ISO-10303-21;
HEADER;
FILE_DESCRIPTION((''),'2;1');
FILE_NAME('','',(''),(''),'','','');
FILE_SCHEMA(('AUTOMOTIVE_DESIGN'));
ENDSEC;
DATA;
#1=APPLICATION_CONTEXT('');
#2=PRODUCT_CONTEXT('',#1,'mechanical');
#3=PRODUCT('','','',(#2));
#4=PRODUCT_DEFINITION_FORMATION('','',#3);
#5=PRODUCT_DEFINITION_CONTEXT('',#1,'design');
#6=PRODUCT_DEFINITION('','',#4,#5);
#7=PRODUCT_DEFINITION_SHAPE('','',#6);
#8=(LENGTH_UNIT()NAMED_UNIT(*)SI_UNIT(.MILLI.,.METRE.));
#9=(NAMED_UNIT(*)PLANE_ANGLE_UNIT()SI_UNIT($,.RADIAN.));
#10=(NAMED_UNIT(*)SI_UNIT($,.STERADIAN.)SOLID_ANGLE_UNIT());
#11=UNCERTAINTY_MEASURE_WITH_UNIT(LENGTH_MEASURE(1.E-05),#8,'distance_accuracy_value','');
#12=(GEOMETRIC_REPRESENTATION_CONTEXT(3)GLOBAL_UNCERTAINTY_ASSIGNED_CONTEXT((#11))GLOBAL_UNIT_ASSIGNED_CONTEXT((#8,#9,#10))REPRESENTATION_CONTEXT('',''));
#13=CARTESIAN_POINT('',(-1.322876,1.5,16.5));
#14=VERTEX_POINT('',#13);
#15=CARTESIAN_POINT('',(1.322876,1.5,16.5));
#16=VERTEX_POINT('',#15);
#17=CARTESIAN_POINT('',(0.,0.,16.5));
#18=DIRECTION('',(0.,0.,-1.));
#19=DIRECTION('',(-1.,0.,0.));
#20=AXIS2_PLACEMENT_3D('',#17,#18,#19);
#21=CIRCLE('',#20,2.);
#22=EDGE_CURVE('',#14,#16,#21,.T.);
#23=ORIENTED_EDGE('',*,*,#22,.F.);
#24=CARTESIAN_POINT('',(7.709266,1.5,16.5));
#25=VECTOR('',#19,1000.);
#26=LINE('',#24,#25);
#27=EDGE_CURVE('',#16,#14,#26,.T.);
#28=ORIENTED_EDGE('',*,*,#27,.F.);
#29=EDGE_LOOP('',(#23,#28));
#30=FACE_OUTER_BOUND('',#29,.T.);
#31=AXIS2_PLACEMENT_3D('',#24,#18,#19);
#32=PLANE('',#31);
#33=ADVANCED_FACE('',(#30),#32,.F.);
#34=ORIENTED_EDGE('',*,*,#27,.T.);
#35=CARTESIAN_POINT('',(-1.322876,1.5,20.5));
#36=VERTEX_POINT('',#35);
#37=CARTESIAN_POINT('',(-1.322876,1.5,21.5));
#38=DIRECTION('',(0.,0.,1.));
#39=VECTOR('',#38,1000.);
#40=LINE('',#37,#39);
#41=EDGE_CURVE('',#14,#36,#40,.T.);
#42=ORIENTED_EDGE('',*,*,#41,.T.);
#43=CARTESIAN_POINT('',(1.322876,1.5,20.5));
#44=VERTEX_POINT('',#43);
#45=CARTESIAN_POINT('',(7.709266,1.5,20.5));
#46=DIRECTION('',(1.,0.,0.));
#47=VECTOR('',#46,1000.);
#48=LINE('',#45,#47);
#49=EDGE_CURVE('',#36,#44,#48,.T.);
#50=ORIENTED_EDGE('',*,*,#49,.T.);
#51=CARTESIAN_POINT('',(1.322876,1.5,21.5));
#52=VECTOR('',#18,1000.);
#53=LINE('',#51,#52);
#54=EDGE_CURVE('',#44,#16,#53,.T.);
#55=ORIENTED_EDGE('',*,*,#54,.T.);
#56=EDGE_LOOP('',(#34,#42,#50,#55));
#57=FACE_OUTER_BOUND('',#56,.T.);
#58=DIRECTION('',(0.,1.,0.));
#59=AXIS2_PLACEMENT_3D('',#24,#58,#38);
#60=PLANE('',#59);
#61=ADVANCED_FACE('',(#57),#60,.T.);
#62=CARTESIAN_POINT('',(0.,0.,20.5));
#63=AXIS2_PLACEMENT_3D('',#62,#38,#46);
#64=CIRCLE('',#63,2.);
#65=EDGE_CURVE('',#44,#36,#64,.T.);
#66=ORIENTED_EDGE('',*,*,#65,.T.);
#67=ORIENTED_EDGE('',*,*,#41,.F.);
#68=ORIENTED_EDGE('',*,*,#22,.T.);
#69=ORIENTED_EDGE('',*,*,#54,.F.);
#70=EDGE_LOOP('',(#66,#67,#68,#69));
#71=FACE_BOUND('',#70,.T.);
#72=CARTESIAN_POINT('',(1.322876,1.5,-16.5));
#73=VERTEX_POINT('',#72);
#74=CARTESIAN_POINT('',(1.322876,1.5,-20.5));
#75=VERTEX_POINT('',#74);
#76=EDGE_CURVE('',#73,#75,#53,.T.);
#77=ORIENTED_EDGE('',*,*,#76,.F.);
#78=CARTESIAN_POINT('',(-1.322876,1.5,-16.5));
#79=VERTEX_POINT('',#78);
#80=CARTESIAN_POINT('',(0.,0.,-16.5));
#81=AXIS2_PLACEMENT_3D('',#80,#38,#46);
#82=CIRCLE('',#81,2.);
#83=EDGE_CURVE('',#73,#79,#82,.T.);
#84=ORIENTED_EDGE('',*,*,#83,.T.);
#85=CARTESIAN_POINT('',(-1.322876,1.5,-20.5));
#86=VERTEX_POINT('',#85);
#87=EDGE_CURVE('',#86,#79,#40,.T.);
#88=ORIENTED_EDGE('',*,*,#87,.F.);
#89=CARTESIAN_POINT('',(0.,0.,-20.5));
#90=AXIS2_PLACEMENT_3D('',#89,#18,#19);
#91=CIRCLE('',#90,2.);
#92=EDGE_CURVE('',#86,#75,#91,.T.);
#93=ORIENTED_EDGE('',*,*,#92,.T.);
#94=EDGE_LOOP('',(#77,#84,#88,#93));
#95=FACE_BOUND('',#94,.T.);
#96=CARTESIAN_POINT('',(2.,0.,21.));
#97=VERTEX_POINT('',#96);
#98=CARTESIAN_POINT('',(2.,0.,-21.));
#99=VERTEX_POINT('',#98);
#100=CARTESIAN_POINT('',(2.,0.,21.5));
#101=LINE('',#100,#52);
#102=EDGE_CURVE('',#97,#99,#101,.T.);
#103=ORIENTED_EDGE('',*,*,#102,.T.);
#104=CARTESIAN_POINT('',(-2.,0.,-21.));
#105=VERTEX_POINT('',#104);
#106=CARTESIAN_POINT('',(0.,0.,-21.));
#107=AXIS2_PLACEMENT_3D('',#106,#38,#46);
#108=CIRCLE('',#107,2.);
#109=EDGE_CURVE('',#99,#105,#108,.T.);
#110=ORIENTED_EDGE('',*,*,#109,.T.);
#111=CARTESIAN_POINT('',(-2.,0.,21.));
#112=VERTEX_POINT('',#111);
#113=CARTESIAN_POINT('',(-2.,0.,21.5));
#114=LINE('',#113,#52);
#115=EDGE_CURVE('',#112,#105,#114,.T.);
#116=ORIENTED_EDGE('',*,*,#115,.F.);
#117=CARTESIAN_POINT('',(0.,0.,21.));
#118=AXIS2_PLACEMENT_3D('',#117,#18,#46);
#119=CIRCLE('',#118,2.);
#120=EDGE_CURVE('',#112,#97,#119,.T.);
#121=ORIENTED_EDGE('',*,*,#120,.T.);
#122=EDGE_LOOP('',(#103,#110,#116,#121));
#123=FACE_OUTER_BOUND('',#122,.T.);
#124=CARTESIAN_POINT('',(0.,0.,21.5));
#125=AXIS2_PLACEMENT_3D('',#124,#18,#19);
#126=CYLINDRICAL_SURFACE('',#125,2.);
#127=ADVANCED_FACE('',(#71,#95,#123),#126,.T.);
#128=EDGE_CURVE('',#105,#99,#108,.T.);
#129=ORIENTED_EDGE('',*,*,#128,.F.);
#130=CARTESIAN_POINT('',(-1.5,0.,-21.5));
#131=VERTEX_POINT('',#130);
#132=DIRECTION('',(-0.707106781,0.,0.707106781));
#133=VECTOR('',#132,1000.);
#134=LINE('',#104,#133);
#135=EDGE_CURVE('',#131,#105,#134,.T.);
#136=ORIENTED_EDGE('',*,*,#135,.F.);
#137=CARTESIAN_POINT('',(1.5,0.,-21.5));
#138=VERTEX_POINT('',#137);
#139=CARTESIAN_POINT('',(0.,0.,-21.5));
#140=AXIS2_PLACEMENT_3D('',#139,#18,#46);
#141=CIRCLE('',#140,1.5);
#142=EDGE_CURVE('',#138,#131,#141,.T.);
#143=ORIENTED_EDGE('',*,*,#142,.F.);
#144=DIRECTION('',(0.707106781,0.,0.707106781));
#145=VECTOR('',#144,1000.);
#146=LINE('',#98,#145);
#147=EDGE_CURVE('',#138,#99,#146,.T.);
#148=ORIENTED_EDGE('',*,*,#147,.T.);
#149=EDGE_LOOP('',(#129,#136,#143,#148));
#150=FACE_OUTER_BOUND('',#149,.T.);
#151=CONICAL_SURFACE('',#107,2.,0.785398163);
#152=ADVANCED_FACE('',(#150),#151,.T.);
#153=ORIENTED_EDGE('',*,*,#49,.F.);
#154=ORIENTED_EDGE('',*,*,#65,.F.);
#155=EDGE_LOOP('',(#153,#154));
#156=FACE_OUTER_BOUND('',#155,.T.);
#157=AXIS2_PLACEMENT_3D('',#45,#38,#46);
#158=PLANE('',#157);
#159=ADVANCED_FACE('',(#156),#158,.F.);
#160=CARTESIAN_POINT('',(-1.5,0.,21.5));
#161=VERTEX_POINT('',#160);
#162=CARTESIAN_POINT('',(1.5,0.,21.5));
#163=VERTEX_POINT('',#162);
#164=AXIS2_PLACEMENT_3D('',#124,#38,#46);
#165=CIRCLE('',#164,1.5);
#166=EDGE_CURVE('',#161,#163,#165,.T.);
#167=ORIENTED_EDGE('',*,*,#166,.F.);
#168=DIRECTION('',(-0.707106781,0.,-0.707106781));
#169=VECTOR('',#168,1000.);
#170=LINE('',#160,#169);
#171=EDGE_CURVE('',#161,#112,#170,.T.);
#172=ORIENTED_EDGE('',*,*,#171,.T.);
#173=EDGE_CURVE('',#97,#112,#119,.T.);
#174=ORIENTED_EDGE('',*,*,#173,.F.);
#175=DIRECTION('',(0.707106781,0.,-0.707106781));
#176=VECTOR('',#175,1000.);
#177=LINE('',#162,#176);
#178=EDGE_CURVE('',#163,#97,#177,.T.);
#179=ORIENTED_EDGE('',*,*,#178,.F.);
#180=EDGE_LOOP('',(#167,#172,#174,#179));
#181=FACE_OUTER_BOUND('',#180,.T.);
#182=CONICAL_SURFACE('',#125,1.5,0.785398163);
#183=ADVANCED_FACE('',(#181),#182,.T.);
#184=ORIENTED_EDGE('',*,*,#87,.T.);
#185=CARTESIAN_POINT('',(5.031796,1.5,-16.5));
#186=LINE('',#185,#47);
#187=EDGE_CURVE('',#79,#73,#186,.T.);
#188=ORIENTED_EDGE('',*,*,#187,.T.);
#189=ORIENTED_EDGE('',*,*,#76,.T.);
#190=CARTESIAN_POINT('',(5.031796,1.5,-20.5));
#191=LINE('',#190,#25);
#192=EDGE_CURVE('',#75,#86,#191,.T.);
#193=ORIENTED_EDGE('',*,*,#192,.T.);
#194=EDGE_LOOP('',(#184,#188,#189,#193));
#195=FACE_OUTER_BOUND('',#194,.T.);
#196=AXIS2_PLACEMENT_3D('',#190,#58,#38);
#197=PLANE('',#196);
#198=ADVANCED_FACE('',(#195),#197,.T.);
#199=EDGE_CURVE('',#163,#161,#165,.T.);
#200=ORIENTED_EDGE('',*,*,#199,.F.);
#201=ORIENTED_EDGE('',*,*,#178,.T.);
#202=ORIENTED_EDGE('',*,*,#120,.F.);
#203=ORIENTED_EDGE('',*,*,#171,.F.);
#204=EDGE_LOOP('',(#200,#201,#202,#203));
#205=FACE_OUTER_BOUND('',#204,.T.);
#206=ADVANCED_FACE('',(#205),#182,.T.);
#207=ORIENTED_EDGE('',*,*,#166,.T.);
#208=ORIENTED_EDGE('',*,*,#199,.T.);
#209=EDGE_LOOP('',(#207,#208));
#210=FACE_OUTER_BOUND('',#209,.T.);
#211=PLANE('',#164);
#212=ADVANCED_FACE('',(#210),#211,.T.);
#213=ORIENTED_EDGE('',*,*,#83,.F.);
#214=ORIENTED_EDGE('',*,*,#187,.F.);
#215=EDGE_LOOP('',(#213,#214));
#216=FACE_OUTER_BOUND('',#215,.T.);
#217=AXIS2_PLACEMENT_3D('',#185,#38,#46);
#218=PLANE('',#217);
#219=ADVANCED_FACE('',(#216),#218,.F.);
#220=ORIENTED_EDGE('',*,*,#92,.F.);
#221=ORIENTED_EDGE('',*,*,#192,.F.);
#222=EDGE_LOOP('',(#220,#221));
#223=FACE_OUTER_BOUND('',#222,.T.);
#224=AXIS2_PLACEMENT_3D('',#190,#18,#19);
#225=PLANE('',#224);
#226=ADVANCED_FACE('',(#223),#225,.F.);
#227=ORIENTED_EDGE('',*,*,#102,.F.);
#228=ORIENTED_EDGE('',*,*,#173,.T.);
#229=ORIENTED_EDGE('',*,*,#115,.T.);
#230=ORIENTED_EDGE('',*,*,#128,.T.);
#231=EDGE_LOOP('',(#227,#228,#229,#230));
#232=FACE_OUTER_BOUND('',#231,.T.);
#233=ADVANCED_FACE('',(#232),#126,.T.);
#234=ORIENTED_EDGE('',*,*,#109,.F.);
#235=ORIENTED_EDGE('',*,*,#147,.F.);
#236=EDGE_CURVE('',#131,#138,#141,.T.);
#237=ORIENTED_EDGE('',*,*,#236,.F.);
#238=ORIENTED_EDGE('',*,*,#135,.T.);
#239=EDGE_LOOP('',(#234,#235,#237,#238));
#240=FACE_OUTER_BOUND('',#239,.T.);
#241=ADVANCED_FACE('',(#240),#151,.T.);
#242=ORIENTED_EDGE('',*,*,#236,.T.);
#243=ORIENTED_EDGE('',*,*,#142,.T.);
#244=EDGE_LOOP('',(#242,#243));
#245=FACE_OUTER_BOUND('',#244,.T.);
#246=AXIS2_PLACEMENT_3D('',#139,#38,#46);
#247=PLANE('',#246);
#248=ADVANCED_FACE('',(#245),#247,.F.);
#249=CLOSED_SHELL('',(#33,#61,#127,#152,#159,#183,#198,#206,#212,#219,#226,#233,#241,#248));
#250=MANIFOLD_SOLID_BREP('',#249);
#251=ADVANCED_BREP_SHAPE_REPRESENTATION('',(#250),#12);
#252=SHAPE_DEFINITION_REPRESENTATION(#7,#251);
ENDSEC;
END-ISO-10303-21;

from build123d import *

# Parameters (mm, degrees)
SKETCH1_R           = 2
BOSS_EXTRUDE1_DEPTH = 21.5
SKETCH2_W           = 15.41853157
SKETCH2_H           = 4
SKETCH2_W_2         = 11.817796653
CUT_EXTRUDE1_DEPTH  = 0.5
CHAMFER1_SIZE       = 0.5


with BuildPart() as part:
    # Sketch1 → Boss-Extrude1 (new, symmetric)
    with BuildSketch(Plane.XY):
        Circle(SKETCH1_R)
    extrude(amount=BOSS_EXTRUDE1_DEPTH, both=True)

    # Sketch2 → Cut-Extrude1 (cut)
    with BuildSketch(Plane(origin=(0, 2, 0), x_dir=(-1, 0, 0), z_dir=(0, 1, 0))):
        with Locations((0, 18.5)):
            Rectangle(SKETCH2_W, SKETCH2_H)
        with Locations((0.877102096, -18.5)):
            Rectangle(SKETCH2_W_2, SKETCH2_H)
    extrude(amount=-CUT_EXTRUDE1_DEPTH, mode=Mode.SUBTRACT)

    # Chamfer1
    chamfer1_edges = [part.edges().sort_by_distance(p)[0] for p in [
        (-2, 0, -21.5),
        (-2, 0, 21.5),
    ]]
    chamfer(chamfer1_edges, length=CHAMFER1_SIZE)


solid = part.part
